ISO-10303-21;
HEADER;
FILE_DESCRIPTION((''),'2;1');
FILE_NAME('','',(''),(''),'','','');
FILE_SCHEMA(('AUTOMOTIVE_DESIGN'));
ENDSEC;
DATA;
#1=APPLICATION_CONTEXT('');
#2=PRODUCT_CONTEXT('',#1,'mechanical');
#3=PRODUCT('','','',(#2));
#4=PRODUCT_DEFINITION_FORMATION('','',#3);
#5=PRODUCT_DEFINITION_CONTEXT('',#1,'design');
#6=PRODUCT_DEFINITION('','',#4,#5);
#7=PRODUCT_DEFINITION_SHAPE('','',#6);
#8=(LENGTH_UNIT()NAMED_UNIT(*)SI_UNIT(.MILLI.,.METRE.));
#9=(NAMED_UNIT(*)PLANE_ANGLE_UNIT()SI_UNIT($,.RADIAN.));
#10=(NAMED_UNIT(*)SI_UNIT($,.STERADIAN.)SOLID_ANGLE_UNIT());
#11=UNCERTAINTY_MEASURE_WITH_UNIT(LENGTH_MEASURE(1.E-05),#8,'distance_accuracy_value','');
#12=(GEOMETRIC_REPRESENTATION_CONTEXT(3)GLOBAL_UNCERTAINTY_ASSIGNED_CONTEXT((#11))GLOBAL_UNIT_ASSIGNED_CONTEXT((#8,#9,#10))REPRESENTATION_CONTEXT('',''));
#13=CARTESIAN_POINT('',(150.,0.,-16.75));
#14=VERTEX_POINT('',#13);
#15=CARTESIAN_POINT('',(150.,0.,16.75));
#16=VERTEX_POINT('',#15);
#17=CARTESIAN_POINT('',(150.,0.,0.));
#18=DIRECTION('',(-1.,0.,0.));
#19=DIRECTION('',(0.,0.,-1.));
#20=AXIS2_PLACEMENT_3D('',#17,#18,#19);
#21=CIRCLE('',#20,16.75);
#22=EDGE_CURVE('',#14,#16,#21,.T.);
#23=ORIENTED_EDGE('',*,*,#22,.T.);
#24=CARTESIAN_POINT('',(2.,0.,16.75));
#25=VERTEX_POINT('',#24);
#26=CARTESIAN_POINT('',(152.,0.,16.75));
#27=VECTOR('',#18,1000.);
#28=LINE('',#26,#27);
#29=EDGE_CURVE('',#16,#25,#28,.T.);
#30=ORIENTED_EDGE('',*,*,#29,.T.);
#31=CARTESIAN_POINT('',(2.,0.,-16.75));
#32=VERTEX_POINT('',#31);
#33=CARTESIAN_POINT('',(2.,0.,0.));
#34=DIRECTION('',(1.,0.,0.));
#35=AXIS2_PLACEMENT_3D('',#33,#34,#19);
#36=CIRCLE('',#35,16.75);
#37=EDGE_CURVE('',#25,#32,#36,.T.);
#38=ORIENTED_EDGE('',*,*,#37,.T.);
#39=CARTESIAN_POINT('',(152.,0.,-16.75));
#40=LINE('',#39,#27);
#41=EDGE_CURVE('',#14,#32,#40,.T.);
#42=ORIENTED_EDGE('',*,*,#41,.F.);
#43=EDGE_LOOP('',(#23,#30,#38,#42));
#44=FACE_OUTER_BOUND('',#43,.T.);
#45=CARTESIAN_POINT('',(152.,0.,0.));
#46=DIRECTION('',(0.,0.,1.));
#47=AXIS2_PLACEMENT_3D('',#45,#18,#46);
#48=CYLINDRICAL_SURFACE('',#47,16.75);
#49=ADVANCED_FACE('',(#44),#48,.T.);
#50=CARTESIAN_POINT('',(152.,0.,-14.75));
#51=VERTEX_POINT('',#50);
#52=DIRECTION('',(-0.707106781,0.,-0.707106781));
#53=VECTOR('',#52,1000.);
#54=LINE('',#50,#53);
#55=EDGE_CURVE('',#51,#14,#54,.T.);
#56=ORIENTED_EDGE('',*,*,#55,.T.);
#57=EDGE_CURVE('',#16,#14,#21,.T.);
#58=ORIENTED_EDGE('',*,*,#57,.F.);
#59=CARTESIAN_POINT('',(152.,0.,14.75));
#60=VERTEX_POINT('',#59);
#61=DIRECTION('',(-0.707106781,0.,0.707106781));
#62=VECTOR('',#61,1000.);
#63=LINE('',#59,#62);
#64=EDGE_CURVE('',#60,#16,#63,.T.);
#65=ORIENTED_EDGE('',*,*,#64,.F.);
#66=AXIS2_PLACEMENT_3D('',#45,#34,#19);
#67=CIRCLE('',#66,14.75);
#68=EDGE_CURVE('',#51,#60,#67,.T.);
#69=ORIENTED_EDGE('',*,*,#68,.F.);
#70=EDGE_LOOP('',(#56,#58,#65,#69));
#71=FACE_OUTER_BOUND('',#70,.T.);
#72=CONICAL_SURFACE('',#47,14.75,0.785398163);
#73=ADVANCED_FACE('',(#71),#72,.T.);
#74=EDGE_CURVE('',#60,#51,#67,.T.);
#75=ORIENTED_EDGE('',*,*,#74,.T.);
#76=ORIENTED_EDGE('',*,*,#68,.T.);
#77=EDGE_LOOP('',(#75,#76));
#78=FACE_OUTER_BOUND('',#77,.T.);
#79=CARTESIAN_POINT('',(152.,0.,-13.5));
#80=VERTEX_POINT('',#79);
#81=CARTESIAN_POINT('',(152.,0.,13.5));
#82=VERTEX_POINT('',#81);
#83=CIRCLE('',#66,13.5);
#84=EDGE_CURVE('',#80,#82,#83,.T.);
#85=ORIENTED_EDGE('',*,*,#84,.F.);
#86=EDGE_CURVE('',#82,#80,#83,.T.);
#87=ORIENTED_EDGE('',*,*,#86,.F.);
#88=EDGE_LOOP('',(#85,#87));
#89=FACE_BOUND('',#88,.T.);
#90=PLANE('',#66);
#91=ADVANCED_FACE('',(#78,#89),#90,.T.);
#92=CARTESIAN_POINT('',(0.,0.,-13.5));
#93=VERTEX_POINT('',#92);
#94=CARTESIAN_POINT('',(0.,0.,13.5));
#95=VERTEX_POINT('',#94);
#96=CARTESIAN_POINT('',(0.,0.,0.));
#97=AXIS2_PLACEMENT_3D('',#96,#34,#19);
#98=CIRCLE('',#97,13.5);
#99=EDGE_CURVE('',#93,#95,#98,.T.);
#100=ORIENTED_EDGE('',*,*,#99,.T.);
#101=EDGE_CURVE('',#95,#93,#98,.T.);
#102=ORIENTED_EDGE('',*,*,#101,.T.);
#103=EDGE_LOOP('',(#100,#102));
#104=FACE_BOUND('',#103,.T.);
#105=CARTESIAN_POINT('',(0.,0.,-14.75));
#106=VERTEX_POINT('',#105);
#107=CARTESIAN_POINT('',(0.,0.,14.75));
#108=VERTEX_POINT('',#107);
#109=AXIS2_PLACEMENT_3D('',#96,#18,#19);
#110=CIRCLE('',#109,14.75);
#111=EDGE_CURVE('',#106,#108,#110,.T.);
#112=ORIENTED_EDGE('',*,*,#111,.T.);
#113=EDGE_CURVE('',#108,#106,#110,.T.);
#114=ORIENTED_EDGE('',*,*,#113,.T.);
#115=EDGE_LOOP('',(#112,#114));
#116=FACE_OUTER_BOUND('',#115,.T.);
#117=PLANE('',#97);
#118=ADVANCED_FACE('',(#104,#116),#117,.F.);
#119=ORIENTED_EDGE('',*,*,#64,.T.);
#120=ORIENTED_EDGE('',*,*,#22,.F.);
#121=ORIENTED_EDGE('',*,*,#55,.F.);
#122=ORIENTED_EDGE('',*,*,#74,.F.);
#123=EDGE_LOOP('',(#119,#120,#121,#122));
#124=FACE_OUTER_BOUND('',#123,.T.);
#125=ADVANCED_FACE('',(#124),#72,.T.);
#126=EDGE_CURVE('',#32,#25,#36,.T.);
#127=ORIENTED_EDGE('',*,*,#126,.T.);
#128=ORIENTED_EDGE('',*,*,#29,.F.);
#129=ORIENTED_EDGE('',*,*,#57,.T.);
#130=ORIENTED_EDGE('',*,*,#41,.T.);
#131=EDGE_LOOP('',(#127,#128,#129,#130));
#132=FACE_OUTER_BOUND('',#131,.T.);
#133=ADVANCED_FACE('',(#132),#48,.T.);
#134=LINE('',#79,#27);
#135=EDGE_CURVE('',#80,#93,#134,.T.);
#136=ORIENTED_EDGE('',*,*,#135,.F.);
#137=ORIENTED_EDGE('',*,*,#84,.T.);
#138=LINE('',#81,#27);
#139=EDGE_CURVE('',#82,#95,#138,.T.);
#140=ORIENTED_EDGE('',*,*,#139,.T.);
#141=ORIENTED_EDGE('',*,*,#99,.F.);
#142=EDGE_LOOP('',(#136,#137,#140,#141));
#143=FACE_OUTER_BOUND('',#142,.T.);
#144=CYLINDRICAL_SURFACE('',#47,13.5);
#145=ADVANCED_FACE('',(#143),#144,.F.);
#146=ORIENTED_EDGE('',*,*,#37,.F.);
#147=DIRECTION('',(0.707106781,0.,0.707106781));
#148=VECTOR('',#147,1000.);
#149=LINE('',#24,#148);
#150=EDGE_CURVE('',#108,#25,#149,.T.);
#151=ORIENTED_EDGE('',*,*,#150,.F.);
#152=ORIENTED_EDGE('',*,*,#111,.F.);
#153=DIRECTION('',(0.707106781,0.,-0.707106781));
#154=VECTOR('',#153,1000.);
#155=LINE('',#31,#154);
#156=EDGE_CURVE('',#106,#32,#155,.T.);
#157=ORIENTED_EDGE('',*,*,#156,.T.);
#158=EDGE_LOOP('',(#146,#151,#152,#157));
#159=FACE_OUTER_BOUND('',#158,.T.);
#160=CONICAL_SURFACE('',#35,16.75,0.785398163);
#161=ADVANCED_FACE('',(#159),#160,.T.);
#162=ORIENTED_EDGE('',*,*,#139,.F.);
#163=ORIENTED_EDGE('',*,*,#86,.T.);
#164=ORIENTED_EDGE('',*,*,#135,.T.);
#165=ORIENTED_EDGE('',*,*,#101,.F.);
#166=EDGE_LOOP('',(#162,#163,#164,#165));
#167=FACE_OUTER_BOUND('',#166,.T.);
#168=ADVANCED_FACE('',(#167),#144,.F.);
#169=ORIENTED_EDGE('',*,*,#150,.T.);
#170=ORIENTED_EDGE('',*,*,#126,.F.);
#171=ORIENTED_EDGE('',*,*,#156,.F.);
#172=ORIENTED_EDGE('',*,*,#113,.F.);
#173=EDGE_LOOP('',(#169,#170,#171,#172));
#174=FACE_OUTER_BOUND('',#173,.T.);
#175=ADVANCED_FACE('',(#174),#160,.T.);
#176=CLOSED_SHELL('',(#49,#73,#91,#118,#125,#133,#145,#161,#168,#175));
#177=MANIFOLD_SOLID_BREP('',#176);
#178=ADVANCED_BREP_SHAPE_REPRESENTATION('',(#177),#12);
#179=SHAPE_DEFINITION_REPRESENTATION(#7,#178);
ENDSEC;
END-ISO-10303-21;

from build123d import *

# Parameters (mm, degrees)
SKETCH_1_R      = 16.75
SKETCH_1_R_2    = 13.5
EXTRUDE_1_DEPTH = 152
CHAMFER_1_SIZE  = 2


with BuildPart() as part:
    # 草图1 → 拉伸-薄壁1 (new body)
    with BuildSketch(Plane(origin=(0, 0, 0), x_dir=(0, 0, -1), z_dir=(1, 0, 0))):
        Circle(SKETCH_1_R)
        Circle(SKETCH_1_R_2, mode=Mode.SUBTRACT)
    extrude(amount=EXTRUDE_1_DEPTH)

    # 倒角1
    chamfer_1_edges = [part.edges().sort_by_distance(p)[0] for p in [
        (0, 0, 16.75),
        (152, 0, 16.75),
    ]]
    chamfer(chamfer_1_edges, length=CHAMFER_1_SIZE)


solid = part.part
